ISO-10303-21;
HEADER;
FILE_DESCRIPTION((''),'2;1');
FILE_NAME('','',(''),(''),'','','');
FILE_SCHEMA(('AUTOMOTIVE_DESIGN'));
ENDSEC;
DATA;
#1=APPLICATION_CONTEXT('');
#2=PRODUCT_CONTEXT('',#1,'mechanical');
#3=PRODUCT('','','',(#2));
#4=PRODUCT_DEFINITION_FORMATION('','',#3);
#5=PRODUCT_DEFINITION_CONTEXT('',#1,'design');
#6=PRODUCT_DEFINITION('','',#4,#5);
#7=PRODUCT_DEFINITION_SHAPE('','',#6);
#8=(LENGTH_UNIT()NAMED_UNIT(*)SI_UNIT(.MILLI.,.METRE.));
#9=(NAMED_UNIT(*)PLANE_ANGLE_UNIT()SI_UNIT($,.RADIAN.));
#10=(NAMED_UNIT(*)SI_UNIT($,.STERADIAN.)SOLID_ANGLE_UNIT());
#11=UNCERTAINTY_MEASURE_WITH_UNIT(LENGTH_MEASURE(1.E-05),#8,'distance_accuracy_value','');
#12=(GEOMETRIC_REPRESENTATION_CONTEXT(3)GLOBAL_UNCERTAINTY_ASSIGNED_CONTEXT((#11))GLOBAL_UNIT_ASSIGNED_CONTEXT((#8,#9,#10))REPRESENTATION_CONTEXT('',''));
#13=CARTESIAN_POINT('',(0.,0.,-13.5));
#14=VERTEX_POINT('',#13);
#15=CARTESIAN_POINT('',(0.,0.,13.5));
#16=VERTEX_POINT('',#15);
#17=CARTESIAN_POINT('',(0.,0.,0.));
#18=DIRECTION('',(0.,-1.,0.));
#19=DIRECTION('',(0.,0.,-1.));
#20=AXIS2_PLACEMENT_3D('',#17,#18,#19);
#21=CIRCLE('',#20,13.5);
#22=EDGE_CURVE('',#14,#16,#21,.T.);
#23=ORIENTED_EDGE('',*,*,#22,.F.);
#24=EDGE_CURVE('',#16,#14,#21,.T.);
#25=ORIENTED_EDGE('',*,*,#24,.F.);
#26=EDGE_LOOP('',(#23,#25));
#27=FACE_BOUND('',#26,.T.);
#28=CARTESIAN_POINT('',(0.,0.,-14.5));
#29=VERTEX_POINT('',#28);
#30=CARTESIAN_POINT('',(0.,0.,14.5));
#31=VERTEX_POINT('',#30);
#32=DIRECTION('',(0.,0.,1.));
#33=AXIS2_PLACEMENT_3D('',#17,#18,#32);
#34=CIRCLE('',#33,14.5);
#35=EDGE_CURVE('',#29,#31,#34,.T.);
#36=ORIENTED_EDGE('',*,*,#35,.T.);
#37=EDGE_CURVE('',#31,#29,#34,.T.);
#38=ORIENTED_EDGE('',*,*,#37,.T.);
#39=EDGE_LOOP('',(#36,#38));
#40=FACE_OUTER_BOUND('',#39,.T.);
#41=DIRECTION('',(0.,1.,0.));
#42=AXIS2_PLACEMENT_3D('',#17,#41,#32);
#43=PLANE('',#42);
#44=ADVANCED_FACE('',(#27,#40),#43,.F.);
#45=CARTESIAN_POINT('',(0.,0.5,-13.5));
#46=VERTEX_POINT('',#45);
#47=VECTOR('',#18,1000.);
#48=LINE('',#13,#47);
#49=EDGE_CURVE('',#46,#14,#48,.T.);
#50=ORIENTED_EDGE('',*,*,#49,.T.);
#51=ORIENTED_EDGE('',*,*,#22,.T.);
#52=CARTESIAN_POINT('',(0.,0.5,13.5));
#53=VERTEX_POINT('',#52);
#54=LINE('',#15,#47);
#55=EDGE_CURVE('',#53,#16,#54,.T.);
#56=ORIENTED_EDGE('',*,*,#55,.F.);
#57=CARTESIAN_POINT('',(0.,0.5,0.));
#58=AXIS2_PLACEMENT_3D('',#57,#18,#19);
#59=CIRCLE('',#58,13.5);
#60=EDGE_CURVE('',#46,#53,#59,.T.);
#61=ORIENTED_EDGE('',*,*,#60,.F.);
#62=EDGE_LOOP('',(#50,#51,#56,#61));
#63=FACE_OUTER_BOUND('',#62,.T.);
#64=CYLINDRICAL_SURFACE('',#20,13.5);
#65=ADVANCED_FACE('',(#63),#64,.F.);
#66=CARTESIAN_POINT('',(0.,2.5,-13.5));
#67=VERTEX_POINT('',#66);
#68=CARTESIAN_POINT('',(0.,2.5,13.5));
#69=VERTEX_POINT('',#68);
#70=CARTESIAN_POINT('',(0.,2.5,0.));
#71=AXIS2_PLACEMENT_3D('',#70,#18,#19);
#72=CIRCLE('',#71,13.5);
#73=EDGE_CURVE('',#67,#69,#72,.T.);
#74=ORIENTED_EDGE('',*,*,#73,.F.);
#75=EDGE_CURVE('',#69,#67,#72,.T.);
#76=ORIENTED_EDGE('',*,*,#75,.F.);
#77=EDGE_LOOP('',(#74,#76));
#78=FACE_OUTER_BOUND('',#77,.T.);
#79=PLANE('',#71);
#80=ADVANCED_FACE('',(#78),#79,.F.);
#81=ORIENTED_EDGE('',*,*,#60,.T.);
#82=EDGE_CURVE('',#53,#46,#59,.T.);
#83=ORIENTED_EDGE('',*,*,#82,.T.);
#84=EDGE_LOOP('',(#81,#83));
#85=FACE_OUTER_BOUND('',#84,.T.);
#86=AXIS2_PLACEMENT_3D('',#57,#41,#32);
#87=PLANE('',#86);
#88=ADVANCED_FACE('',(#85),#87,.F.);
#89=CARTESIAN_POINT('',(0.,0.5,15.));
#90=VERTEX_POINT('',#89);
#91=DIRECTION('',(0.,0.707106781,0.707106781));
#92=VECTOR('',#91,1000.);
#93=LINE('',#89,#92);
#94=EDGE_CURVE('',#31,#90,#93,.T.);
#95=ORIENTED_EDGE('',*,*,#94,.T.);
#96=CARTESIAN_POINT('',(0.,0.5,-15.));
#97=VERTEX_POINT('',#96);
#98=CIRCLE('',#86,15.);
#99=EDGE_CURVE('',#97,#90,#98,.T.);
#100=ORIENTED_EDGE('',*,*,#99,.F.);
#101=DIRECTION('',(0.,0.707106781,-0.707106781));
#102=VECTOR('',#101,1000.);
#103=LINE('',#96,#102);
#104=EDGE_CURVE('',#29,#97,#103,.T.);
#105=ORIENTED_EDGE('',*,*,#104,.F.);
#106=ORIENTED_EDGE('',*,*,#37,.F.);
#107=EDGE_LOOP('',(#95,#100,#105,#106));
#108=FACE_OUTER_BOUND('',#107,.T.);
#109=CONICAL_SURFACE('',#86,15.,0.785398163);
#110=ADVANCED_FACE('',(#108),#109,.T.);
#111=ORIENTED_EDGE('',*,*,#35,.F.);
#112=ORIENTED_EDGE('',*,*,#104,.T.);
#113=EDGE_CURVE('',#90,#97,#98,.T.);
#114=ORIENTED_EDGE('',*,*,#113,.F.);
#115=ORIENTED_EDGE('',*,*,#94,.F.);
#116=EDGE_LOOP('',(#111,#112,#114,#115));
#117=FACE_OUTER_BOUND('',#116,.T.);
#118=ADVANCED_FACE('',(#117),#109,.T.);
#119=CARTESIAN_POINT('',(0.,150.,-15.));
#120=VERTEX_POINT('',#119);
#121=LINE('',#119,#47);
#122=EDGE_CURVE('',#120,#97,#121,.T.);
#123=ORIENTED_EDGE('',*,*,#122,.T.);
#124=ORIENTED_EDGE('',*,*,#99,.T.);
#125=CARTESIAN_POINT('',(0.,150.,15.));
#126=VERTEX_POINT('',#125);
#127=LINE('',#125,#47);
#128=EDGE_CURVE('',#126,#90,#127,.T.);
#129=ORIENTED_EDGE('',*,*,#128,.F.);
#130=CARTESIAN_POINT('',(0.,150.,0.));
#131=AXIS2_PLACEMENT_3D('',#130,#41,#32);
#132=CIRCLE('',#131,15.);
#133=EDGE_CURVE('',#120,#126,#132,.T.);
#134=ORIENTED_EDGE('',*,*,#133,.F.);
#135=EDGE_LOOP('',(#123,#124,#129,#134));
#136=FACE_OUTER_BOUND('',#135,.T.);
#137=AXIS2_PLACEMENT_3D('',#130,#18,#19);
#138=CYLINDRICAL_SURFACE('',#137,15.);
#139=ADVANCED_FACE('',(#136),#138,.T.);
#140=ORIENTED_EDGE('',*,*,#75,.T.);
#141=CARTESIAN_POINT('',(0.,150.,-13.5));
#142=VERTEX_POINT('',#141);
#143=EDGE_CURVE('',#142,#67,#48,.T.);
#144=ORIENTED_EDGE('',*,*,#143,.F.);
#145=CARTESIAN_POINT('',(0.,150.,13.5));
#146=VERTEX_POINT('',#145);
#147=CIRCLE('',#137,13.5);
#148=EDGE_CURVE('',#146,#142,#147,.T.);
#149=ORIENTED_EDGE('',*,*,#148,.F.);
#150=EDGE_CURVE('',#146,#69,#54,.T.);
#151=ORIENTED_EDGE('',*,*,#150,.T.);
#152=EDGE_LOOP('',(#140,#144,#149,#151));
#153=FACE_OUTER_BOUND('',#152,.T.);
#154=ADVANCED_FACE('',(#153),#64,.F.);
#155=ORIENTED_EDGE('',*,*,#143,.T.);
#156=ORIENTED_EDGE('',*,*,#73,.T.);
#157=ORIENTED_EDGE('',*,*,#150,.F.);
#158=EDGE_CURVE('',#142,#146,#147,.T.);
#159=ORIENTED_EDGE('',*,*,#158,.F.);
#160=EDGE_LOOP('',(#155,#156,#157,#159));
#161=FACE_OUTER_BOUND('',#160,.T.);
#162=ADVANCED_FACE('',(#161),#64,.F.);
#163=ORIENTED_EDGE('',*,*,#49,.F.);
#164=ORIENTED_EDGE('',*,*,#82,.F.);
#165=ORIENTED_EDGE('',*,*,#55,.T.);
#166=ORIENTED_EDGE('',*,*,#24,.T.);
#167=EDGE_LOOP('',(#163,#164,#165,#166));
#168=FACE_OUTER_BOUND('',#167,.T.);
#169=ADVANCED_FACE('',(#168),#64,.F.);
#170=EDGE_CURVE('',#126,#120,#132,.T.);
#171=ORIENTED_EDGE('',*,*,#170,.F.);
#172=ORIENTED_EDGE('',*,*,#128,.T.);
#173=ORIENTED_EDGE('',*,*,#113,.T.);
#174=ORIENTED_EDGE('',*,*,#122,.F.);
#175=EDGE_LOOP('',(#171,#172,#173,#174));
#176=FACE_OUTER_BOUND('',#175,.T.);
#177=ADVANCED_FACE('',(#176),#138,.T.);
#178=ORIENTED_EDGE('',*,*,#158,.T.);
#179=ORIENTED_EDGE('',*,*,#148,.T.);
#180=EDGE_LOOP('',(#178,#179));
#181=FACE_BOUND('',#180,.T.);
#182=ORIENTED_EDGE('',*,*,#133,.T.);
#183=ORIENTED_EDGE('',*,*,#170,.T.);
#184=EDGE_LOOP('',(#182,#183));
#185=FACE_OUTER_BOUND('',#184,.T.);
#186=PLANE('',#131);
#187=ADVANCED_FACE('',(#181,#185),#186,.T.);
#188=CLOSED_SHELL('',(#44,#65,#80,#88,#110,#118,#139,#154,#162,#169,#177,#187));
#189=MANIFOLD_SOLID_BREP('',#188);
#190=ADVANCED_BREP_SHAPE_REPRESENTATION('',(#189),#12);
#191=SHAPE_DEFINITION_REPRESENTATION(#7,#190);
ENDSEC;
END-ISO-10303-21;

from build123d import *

# Parameters (mm, degrees)
SKETCH1_R           = 15
BOSS_EXTRUDE1_DEPTH = 150
SKETCH3_W           = 13.5
SKETCH3_H           = 147.5
SKETCH3_H_2         = 0.5
CHAMFER1_SIZE       = 0.5


with BuildPart() as part:
    # Sketch1 → Boss-Extrude1 (new body)
    with BuildSketch(Plane(origin=(0, 0, 0), x_dir=(1, 0, 0), z_dir=(0, 1, 0))):
        with Locations(Location((0, 0, 0), (0, 0, 270))):
            Circle(SKETCH1_R)
    extrude(amount=BOSS_EXTRUDE1_DEPTH)

    # Sketch3 → Cut-Revolve1 (revolve, cut)
    with BuildSketch(Plane.XY, mode=Mode.PRIVATE) as cut_revolve1_sk:
        with Locations((6.75, 76.25)):
            Rectangle(SKETCH3_W, SKETCH3_H)
        with Locations((6.75, 0.25)):
            Rectangle(SKETCH3_W, SKETCH3_H_2)
    revolve(cut_revolve1_sk.sketch.rotate(Axis((0, 0, 0), (0, 1, 0)), 90), axis=Axis((0, 0, 0), (0, 1, 0)), mode=Mode.SUBTRACT)

    # Chamfer1
    chamfer1_edges = [part.edges().sort_by_distance(p)[0] for p in [
        (0, 0, -15),
    ]]
    chamfer(chamfer1_edges, length=CHAMFER1_SIZE)


solid = part.part
